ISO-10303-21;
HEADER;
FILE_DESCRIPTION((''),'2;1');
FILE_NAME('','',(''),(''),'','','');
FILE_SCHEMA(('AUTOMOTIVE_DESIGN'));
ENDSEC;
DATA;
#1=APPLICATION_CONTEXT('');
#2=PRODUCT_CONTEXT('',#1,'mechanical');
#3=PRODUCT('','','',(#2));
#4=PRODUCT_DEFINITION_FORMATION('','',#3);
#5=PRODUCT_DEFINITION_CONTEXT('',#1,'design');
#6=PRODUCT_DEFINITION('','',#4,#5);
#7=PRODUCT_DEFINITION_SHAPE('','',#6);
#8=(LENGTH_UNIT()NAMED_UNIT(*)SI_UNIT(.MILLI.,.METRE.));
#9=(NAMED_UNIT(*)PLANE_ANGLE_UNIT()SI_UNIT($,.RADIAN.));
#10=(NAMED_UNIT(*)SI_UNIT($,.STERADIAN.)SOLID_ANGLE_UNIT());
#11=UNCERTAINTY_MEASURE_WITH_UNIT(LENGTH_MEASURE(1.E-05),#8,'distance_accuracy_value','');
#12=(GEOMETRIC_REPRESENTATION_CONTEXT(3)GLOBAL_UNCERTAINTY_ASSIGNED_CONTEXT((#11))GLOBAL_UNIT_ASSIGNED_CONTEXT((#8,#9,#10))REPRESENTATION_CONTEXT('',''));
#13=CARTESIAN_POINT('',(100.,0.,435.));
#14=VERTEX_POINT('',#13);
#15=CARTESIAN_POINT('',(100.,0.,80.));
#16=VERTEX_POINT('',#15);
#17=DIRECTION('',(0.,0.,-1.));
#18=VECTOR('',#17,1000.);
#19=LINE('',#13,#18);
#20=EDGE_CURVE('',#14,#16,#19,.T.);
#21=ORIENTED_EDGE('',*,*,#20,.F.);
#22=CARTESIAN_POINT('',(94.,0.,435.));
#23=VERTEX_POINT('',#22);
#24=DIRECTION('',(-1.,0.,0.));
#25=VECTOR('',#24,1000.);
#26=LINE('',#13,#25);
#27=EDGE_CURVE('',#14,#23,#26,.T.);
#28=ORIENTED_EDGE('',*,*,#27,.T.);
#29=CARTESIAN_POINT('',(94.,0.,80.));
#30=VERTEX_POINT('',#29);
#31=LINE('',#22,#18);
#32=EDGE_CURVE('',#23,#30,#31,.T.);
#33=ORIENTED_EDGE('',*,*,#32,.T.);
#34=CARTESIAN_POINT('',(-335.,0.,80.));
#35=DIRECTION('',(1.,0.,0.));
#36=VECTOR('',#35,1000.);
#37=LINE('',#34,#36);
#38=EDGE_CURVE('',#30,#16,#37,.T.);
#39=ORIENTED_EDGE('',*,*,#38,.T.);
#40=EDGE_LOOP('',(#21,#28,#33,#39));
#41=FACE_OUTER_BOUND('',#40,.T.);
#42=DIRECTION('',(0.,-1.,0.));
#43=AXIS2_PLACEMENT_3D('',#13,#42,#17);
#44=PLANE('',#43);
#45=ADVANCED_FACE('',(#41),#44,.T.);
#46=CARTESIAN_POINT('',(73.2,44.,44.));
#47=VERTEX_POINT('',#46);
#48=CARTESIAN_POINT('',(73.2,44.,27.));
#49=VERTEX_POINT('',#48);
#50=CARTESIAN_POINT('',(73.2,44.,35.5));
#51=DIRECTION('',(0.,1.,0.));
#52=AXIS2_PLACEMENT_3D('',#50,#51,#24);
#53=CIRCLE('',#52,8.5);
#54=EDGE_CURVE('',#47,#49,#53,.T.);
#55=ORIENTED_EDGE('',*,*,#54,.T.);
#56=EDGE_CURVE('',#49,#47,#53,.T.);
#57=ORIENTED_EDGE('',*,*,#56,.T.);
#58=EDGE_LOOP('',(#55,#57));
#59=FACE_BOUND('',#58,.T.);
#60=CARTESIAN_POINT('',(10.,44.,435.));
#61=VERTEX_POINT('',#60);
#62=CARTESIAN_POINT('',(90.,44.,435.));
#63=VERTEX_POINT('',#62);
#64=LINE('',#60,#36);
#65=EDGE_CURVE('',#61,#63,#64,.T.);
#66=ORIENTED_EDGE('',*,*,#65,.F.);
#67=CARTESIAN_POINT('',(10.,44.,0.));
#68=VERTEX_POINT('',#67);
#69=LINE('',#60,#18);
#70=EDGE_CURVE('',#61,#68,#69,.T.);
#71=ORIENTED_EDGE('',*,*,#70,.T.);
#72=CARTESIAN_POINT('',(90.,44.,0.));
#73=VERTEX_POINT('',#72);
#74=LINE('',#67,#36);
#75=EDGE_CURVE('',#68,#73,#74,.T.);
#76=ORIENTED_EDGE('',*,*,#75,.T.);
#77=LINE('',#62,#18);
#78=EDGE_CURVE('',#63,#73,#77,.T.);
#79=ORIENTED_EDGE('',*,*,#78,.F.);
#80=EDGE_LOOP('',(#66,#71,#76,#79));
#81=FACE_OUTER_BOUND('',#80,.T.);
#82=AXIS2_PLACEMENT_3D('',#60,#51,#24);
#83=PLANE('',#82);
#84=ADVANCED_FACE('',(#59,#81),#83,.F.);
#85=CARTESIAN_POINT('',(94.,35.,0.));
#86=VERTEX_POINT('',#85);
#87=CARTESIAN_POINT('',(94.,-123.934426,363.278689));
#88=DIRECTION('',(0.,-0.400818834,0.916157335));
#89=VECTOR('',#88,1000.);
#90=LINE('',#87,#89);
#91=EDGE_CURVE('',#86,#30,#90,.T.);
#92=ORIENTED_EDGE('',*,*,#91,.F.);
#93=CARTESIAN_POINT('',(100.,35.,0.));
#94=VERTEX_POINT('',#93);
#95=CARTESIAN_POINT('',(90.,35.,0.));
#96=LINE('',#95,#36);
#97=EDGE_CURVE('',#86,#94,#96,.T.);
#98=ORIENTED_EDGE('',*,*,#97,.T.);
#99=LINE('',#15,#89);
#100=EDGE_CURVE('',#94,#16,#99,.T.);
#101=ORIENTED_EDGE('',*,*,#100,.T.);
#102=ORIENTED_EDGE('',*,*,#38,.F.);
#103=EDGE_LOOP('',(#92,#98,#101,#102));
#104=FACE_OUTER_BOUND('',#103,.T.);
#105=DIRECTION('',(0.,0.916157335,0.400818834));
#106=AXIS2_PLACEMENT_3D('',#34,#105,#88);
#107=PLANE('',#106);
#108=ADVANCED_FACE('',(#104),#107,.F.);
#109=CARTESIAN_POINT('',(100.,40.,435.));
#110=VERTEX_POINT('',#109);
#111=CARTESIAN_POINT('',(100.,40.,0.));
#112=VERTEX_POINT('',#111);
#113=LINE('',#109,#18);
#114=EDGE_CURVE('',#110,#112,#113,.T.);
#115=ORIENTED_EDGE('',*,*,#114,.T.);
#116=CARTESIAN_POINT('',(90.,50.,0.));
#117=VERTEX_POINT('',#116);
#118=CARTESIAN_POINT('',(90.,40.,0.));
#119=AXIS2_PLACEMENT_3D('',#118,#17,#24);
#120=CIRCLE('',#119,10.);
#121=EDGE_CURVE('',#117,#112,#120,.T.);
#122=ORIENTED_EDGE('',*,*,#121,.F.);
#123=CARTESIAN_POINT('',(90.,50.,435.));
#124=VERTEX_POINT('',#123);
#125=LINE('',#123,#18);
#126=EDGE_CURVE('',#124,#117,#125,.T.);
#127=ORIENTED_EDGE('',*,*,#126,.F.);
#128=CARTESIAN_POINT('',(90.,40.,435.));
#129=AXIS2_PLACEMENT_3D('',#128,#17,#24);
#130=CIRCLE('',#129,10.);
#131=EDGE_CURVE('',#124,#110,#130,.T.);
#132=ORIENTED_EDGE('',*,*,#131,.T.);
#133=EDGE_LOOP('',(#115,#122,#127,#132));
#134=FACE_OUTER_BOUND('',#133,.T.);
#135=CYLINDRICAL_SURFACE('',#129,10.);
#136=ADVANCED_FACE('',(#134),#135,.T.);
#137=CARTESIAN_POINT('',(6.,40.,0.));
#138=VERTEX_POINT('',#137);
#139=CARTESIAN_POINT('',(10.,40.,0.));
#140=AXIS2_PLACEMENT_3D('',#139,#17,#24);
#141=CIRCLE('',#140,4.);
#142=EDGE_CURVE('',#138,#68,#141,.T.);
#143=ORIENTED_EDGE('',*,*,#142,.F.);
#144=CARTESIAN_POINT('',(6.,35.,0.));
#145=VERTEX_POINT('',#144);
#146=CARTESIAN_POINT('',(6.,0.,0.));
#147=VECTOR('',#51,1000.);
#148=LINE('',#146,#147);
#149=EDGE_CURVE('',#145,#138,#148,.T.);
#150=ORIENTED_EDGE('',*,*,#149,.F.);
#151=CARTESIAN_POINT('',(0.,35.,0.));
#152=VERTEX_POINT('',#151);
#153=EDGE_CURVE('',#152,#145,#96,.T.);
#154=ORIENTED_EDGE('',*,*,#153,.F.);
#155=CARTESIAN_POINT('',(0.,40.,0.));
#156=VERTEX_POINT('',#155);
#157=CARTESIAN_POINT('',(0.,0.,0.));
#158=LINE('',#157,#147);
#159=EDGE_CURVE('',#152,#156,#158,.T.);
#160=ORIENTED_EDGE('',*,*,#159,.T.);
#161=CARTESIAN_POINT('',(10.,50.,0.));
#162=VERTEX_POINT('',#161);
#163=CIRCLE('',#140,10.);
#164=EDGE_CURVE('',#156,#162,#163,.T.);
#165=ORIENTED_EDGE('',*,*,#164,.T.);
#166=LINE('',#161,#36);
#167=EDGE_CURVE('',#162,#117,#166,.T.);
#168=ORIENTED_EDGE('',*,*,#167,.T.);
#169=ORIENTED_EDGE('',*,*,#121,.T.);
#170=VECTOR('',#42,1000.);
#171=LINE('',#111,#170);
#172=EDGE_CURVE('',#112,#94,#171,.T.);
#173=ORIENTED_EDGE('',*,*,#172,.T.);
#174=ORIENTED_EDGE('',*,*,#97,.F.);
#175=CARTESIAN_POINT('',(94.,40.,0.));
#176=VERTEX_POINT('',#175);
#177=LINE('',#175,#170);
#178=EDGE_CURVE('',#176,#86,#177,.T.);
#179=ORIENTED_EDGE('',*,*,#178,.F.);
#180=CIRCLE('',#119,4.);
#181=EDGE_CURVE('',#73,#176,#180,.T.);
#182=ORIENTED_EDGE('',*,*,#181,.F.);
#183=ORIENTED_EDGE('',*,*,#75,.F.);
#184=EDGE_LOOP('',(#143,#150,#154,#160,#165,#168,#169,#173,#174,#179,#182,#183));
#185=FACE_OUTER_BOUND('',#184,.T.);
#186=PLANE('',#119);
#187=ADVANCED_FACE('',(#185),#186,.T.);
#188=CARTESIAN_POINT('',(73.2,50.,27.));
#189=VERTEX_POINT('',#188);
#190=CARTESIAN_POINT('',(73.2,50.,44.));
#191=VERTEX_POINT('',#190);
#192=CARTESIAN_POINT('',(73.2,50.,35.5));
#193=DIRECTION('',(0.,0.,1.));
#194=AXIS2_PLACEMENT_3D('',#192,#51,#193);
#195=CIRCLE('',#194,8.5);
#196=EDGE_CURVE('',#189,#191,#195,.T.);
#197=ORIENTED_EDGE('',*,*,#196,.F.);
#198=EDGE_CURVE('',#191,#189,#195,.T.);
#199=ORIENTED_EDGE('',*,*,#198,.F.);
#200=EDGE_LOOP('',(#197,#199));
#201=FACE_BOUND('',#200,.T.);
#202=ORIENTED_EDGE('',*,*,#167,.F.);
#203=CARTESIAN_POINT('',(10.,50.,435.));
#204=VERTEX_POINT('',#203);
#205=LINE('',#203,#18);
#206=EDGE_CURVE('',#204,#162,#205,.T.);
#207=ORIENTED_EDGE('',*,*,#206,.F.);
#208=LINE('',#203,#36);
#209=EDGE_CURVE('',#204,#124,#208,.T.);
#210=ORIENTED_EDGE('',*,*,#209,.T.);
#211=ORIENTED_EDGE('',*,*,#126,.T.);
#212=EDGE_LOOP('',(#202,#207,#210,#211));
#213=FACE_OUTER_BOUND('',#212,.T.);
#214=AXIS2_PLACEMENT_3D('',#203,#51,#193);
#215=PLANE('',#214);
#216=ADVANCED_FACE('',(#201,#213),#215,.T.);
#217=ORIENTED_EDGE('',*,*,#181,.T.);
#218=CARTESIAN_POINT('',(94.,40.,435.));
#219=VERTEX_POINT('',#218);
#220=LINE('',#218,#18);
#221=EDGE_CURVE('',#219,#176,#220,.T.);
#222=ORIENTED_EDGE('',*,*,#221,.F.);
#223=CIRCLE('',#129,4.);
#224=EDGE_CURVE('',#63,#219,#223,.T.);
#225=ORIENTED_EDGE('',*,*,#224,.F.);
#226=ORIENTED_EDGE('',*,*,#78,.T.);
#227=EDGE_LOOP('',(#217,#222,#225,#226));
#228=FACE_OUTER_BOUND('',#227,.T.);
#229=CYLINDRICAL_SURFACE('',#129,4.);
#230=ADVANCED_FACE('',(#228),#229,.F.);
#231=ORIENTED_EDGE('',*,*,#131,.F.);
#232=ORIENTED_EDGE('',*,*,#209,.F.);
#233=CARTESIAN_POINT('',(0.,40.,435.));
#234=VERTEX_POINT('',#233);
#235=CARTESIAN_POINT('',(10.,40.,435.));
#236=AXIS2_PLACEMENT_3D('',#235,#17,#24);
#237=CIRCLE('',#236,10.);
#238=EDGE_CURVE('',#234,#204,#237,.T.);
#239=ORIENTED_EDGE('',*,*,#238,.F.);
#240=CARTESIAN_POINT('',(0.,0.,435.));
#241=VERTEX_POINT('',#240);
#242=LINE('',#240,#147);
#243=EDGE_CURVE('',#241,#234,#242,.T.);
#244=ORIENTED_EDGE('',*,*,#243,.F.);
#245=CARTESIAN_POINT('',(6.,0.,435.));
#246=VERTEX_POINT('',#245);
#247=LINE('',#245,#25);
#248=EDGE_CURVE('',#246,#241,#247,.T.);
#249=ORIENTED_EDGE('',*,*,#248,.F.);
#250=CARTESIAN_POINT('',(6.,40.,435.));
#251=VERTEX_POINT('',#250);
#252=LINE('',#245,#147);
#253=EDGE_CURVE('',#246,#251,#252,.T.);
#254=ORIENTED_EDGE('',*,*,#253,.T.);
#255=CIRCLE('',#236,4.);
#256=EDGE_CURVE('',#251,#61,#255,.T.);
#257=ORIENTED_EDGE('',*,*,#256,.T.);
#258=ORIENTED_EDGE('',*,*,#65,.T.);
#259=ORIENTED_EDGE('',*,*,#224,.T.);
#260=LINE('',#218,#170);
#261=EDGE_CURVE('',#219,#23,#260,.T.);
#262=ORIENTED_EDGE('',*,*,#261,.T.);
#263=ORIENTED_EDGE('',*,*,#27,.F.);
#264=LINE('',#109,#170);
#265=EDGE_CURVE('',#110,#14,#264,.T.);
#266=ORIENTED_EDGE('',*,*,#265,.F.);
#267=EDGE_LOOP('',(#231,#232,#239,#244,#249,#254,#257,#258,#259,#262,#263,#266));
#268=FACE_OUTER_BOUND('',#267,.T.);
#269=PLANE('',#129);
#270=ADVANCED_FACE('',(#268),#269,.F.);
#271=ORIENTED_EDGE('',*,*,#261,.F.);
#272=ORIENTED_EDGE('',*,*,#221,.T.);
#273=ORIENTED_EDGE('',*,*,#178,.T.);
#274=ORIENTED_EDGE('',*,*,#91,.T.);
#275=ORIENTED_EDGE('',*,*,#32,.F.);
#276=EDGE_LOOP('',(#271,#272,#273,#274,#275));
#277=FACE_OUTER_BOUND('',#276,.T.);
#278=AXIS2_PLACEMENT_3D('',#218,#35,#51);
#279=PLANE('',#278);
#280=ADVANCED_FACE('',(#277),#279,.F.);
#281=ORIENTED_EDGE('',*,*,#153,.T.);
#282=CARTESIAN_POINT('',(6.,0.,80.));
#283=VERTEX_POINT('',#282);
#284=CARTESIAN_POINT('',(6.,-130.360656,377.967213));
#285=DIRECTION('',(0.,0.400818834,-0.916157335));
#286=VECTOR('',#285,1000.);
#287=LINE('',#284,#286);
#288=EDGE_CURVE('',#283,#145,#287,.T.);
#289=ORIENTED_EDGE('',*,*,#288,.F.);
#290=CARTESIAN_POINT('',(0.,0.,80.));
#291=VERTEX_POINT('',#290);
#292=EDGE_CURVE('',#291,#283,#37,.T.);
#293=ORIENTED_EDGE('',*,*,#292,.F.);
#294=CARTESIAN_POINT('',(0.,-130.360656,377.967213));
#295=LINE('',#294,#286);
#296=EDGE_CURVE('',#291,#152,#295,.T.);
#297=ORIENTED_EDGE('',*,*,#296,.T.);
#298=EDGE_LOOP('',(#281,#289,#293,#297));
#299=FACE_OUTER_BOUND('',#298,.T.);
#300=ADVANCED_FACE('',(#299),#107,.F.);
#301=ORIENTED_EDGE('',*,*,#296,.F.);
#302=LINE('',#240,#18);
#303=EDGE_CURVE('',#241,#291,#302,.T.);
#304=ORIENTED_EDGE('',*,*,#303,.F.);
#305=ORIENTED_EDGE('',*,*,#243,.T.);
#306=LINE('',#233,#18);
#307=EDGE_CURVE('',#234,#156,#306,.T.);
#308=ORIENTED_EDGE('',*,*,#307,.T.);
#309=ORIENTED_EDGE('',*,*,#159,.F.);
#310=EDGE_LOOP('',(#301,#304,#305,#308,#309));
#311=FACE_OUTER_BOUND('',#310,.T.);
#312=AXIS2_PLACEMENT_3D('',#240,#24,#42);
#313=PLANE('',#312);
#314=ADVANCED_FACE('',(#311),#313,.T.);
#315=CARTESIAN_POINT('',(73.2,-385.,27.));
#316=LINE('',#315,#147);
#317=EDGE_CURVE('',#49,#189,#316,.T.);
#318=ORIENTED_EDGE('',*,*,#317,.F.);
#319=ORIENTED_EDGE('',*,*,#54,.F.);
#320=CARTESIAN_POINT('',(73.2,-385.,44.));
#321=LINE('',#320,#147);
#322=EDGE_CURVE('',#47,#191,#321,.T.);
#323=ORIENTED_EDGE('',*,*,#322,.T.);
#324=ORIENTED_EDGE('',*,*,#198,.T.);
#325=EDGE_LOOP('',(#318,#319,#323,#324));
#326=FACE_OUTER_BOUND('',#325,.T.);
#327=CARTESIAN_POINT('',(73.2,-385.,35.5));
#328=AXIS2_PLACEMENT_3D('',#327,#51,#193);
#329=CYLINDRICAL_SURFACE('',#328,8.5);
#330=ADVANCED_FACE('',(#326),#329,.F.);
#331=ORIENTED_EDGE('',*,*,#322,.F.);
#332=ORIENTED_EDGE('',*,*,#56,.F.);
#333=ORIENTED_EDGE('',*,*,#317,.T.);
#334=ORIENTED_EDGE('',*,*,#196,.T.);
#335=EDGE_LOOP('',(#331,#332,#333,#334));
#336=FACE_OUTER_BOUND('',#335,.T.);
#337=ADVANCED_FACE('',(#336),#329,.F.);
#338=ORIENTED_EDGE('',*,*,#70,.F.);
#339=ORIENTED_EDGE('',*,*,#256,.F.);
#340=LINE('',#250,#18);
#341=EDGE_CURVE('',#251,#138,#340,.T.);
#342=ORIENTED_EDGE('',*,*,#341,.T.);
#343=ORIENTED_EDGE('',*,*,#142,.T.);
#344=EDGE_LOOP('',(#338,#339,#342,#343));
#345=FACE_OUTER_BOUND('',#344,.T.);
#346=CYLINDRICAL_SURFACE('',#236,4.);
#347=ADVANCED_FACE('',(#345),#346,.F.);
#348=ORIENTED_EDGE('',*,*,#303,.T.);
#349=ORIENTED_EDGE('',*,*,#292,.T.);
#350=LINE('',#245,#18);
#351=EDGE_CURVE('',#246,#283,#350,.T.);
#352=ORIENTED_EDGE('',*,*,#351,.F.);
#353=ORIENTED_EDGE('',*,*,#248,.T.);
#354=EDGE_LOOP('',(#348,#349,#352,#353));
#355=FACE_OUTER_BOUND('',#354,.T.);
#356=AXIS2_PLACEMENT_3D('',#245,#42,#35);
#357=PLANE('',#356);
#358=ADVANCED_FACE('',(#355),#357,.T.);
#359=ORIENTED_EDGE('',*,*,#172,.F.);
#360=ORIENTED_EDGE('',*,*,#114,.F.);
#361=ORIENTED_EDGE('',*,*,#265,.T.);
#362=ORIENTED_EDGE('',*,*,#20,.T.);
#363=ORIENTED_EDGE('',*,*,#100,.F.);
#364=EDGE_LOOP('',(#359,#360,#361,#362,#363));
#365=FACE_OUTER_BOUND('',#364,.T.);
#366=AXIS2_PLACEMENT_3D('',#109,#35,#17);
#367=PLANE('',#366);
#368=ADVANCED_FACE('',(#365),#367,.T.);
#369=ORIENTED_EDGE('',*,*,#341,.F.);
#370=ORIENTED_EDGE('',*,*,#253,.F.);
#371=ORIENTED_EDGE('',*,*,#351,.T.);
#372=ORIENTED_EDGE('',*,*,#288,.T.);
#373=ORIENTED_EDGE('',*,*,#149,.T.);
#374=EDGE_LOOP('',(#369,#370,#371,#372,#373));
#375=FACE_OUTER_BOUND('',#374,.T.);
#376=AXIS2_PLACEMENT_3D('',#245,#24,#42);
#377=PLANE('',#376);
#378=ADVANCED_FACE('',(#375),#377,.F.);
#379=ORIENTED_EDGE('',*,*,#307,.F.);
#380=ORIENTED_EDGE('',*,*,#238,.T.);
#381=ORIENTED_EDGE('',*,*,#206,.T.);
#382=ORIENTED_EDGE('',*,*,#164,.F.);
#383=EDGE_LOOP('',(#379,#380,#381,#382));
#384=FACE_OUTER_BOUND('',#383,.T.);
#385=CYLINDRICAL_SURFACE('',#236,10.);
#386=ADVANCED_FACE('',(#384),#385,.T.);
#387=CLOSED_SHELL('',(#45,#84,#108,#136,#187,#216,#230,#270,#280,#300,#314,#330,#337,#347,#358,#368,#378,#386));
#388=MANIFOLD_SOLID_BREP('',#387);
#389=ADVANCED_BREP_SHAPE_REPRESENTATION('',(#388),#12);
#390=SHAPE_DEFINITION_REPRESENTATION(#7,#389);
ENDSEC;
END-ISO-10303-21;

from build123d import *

# Parameters (mm, degrees)
BOSS_EXTRUDE1_DEPTH = 435
SKETCH2_R           = 8.5
CUT_EXTRUDE1_DEPTH  = 435
CUT_EXTRUDE2_DEPTH  = 435


with BuildPart() as part:
    # Sketch1 → Boss-Extrude1 (new body)
    with BuildSketch(Plane.XY):
        with BuildLine():
            Line((0, 0), (0, 40))
            ThreePointArc((0, 40), (2.928932188, 47.071067812), (10, 50))
            Line((10, 50), (90, 50))
            ThreePointArc((90, 50), (97.071067812, 47.071067812), (100, 40))
            Line((100, 40), (100, 0))
            Line((100, 0), (94, 0))
            Line((94, 0), (94, 40))
            ThreePointArc((94, 40), (92.828427125, 42.828427125), (90, 44))
            Line((90, 44), (10, 44))
            ThreePointArc((10, 44), (7.171572875, 42.828427125), (6, 40))
            Line((6, 40), (6, 0))
            Line((6, 0), (0, 0))
        make_face()
    extrude(amount=BOSS_EXTRUDE1_DEPTH)

    # Sketch2 → Cut-Extrude1 (cut)
    with BuildSketch(Plane(origin=(0, 50, 0), x_dir=(1, 0, 0), z_dir=(0, 1, 0))):
        with Locations(Location((73.2, -35.5, 0), (0, 0, 270))):
            Circle(SKETCH2_R)
    extrude(amount=-CUT_EXTRUDE1_DEPTH, mode=Mode.SUBTRACT)

    # Sketch3 → Cut-Extrude2 (cut)
    with BuildSketch(Plane(origin=(100, 0, 0), x_dir=(0, 0, -1), z_dir=(1, 0, 0))):
        Polygon((-80, 0), (0, 35), (0, 0), align=None)
    extrude(amount=-CUT_EXTRUDE2_DEPTH, mode=Mode.SUBTRACT)


solid = part.part
